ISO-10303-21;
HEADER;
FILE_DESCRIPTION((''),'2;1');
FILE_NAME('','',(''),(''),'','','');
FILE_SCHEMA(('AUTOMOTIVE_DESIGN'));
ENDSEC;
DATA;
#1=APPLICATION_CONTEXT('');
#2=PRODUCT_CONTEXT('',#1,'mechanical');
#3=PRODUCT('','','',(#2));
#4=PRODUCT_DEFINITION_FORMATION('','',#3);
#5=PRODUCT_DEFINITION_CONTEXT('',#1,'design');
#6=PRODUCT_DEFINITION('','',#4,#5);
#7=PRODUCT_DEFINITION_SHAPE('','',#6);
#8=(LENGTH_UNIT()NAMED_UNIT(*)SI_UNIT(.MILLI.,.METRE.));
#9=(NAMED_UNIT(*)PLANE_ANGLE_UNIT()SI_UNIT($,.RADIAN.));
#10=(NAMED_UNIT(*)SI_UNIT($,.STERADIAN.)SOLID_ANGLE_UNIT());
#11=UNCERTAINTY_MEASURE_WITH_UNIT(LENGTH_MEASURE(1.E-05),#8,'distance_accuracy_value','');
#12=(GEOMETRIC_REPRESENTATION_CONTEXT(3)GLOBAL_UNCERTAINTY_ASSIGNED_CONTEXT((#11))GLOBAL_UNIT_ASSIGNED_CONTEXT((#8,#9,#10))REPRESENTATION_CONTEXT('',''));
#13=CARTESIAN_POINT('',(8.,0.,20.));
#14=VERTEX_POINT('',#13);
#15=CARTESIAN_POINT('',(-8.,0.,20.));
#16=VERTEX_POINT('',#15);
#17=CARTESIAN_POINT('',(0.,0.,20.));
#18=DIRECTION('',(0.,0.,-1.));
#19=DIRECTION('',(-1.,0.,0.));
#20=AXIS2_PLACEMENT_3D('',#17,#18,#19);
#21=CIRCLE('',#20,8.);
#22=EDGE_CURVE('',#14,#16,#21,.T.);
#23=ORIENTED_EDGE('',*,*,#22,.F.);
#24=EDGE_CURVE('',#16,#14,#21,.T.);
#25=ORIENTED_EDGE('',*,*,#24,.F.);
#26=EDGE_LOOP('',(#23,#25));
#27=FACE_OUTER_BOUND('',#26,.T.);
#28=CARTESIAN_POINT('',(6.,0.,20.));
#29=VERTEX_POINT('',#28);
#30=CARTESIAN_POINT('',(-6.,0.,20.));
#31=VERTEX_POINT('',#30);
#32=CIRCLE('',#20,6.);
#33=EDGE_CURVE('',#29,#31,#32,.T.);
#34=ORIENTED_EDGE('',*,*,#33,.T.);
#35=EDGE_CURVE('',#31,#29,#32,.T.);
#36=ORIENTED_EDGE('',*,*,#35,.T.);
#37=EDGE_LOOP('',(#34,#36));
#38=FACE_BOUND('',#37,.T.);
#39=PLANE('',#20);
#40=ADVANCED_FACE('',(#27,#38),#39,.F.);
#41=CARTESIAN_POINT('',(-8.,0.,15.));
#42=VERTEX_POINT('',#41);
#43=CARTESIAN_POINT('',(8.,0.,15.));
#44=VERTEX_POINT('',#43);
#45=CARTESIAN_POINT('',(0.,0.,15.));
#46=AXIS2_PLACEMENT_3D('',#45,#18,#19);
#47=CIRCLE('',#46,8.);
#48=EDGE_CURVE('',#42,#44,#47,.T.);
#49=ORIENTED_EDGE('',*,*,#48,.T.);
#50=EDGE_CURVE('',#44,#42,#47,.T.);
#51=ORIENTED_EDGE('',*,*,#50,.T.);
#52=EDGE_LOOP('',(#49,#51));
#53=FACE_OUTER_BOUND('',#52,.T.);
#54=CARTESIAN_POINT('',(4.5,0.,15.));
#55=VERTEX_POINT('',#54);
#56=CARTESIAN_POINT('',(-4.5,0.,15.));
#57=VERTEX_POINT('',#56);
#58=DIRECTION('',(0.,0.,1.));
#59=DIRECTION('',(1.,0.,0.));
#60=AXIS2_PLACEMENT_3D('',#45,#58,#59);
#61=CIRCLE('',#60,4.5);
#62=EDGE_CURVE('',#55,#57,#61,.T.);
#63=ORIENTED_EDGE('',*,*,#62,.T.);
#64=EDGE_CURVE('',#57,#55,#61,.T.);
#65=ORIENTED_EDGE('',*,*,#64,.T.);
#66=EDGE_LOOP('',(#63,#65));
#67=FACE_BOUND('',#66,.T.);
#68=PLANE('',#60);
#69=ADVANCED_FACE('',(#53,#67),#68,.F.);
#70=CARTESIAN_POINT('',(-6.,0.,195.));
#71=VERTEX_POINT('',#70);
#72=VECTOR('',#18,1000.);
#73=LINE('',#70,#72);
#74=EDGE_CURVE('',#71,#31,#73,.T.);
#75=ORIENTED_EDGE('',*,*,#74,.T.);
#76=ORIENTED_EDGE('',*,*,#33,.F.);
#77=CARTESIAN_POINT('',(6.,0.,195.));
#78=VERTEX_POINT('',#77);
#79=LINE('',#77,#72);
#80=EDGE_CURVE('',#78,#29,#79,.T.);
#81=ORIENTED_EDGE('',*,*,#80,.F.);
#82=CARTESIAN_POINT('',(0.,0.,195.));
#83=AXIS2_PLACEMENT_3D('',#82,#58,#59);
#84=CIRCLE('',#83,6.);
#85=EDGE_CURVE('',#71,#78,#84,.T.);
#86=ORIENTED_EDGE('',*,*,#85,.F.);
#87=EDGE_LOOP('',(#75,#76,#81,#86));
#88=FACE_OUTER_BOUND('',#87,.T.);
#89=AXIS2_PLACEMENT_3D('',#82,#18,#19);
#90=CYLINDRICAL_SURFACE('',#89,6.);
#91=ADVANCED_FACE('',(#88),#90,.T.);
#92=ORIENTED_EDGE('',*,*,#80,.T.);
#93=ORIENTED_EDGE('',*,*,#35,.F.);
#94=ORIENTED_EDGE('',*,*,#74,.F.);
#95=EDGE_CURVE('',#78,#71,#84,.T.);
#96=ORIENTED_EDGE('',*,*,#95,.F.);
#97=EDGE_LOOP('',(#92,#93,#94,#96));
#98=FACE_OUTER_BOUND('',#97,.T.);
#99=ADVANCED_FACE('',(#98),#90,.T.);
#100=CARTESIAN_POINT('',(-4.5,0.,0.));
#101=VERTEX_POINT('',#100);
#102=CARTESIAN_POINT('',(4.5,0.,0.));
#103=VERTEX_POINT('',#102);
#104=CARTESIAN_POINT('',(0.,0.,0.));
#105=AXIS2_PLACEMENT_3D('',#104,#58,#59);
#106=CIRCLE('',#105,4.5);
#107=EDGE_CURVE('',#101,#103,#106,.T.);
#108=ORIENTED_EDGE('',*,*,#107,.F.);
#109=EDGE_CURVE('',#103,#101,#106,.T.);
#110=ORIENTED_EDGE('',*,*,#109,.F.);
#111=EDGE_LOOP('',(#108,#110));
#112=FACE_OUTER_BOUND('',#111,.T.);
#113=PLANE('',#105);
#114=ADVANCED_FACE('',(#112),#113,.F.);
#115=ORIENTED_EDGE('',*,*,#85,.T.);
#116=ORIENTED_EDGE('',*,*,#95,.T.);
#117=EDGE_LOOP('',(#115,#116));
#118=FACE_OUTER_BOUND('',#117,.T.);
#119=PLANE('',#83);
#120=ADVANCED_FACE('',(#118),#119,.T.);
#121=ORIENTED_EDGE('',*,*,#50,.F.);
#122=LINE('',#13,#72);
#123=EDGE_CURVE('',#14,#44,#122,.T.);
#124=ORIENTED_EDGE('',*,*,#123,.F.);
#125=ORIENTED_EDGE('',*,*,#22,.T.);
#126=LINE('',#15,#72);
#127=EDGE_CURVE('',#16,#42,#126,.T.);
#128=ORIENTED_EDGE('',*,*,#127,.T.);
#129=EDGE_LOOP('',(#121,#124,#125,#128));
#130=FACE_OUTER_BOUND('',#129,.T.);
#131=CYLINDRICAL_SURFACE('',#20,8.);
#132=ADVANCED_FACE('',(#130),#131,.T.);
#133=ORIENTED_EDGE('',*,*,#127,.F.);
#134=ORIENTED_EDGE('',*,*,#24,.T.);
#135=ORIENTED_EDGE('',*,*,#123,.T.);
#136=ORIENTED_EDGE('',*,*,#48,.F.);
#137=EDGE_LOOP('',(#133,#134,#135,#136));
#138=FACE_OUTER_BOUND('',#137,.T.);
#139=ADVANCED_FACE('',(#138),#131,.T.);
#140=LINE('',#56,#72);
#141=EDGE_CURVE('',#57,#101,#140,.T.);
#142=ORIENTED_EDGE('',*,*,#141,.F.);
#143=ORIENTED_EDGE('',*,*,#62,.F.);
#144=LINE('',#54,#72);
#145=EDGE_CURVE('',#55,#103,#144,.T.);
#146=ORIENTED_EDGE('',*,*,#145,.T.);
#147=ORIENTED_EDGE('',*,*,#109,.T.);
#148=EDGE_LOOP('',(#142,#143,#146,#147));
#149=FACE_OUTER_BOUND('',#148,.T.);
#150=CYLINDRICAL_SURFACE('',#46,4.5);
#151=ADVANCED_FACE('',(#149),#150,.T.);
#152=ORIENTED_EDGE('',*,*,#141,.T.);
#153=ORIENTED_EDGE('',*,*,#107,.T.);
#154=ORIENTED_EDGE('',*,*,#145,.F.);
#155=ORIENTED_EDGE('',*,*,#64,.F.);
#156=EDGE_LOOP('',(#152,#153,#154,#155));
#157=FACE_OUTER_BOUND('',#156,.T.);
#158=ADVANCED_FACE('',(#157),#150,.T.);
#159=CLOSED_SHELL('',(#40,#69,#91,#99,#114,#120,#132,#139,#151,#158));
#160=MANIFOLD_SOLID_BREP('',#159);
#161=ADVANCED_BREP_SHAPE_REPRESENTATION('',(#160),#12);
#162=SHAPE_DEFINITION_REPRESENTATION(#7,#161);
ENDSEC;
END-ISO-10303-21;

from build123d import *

# Parameters (mm, degrees)
SKETCH_1_R      = 4.5
EXTRUDE_1_DEPTH = 15
SKETCH_2_R      = 6
EXTRUDE_2_DEPTH = 180
SKETCH_3_R      = 8
EXTRUDE_3_DEPTH = 5


with BuildPart() as part:
    # 草图1 → 凸台-拉伸1 (new body)
    with BuildSketch(Plane.XY):
        Circle(SKETCH_1_R)
    extrude(amount=EXTRUDE_1_DEPTH)

    # 草图2 → 凸台-拉伸2 (add)
    with BuildSketch(Plane.XY.offset(15)):
        with Locations(Location((0, 0, 0), (0, 0, 180))):
            Circle(SKETCH_2_R)
    extrude(amount=EXTRUDE_2_DEPTH)

    # 草图3 → 凸台-拉伸3 (add)
    with BuildSketch(Plane(origin=(0, 0, 15), x_dir=(-1, 0, 0), z_dir=(0, 0, -1))):
        Circle(SKETCH_3_R)
    extrude(amount=-EXTRUDE_3_DEPTH)


solid = part.part
